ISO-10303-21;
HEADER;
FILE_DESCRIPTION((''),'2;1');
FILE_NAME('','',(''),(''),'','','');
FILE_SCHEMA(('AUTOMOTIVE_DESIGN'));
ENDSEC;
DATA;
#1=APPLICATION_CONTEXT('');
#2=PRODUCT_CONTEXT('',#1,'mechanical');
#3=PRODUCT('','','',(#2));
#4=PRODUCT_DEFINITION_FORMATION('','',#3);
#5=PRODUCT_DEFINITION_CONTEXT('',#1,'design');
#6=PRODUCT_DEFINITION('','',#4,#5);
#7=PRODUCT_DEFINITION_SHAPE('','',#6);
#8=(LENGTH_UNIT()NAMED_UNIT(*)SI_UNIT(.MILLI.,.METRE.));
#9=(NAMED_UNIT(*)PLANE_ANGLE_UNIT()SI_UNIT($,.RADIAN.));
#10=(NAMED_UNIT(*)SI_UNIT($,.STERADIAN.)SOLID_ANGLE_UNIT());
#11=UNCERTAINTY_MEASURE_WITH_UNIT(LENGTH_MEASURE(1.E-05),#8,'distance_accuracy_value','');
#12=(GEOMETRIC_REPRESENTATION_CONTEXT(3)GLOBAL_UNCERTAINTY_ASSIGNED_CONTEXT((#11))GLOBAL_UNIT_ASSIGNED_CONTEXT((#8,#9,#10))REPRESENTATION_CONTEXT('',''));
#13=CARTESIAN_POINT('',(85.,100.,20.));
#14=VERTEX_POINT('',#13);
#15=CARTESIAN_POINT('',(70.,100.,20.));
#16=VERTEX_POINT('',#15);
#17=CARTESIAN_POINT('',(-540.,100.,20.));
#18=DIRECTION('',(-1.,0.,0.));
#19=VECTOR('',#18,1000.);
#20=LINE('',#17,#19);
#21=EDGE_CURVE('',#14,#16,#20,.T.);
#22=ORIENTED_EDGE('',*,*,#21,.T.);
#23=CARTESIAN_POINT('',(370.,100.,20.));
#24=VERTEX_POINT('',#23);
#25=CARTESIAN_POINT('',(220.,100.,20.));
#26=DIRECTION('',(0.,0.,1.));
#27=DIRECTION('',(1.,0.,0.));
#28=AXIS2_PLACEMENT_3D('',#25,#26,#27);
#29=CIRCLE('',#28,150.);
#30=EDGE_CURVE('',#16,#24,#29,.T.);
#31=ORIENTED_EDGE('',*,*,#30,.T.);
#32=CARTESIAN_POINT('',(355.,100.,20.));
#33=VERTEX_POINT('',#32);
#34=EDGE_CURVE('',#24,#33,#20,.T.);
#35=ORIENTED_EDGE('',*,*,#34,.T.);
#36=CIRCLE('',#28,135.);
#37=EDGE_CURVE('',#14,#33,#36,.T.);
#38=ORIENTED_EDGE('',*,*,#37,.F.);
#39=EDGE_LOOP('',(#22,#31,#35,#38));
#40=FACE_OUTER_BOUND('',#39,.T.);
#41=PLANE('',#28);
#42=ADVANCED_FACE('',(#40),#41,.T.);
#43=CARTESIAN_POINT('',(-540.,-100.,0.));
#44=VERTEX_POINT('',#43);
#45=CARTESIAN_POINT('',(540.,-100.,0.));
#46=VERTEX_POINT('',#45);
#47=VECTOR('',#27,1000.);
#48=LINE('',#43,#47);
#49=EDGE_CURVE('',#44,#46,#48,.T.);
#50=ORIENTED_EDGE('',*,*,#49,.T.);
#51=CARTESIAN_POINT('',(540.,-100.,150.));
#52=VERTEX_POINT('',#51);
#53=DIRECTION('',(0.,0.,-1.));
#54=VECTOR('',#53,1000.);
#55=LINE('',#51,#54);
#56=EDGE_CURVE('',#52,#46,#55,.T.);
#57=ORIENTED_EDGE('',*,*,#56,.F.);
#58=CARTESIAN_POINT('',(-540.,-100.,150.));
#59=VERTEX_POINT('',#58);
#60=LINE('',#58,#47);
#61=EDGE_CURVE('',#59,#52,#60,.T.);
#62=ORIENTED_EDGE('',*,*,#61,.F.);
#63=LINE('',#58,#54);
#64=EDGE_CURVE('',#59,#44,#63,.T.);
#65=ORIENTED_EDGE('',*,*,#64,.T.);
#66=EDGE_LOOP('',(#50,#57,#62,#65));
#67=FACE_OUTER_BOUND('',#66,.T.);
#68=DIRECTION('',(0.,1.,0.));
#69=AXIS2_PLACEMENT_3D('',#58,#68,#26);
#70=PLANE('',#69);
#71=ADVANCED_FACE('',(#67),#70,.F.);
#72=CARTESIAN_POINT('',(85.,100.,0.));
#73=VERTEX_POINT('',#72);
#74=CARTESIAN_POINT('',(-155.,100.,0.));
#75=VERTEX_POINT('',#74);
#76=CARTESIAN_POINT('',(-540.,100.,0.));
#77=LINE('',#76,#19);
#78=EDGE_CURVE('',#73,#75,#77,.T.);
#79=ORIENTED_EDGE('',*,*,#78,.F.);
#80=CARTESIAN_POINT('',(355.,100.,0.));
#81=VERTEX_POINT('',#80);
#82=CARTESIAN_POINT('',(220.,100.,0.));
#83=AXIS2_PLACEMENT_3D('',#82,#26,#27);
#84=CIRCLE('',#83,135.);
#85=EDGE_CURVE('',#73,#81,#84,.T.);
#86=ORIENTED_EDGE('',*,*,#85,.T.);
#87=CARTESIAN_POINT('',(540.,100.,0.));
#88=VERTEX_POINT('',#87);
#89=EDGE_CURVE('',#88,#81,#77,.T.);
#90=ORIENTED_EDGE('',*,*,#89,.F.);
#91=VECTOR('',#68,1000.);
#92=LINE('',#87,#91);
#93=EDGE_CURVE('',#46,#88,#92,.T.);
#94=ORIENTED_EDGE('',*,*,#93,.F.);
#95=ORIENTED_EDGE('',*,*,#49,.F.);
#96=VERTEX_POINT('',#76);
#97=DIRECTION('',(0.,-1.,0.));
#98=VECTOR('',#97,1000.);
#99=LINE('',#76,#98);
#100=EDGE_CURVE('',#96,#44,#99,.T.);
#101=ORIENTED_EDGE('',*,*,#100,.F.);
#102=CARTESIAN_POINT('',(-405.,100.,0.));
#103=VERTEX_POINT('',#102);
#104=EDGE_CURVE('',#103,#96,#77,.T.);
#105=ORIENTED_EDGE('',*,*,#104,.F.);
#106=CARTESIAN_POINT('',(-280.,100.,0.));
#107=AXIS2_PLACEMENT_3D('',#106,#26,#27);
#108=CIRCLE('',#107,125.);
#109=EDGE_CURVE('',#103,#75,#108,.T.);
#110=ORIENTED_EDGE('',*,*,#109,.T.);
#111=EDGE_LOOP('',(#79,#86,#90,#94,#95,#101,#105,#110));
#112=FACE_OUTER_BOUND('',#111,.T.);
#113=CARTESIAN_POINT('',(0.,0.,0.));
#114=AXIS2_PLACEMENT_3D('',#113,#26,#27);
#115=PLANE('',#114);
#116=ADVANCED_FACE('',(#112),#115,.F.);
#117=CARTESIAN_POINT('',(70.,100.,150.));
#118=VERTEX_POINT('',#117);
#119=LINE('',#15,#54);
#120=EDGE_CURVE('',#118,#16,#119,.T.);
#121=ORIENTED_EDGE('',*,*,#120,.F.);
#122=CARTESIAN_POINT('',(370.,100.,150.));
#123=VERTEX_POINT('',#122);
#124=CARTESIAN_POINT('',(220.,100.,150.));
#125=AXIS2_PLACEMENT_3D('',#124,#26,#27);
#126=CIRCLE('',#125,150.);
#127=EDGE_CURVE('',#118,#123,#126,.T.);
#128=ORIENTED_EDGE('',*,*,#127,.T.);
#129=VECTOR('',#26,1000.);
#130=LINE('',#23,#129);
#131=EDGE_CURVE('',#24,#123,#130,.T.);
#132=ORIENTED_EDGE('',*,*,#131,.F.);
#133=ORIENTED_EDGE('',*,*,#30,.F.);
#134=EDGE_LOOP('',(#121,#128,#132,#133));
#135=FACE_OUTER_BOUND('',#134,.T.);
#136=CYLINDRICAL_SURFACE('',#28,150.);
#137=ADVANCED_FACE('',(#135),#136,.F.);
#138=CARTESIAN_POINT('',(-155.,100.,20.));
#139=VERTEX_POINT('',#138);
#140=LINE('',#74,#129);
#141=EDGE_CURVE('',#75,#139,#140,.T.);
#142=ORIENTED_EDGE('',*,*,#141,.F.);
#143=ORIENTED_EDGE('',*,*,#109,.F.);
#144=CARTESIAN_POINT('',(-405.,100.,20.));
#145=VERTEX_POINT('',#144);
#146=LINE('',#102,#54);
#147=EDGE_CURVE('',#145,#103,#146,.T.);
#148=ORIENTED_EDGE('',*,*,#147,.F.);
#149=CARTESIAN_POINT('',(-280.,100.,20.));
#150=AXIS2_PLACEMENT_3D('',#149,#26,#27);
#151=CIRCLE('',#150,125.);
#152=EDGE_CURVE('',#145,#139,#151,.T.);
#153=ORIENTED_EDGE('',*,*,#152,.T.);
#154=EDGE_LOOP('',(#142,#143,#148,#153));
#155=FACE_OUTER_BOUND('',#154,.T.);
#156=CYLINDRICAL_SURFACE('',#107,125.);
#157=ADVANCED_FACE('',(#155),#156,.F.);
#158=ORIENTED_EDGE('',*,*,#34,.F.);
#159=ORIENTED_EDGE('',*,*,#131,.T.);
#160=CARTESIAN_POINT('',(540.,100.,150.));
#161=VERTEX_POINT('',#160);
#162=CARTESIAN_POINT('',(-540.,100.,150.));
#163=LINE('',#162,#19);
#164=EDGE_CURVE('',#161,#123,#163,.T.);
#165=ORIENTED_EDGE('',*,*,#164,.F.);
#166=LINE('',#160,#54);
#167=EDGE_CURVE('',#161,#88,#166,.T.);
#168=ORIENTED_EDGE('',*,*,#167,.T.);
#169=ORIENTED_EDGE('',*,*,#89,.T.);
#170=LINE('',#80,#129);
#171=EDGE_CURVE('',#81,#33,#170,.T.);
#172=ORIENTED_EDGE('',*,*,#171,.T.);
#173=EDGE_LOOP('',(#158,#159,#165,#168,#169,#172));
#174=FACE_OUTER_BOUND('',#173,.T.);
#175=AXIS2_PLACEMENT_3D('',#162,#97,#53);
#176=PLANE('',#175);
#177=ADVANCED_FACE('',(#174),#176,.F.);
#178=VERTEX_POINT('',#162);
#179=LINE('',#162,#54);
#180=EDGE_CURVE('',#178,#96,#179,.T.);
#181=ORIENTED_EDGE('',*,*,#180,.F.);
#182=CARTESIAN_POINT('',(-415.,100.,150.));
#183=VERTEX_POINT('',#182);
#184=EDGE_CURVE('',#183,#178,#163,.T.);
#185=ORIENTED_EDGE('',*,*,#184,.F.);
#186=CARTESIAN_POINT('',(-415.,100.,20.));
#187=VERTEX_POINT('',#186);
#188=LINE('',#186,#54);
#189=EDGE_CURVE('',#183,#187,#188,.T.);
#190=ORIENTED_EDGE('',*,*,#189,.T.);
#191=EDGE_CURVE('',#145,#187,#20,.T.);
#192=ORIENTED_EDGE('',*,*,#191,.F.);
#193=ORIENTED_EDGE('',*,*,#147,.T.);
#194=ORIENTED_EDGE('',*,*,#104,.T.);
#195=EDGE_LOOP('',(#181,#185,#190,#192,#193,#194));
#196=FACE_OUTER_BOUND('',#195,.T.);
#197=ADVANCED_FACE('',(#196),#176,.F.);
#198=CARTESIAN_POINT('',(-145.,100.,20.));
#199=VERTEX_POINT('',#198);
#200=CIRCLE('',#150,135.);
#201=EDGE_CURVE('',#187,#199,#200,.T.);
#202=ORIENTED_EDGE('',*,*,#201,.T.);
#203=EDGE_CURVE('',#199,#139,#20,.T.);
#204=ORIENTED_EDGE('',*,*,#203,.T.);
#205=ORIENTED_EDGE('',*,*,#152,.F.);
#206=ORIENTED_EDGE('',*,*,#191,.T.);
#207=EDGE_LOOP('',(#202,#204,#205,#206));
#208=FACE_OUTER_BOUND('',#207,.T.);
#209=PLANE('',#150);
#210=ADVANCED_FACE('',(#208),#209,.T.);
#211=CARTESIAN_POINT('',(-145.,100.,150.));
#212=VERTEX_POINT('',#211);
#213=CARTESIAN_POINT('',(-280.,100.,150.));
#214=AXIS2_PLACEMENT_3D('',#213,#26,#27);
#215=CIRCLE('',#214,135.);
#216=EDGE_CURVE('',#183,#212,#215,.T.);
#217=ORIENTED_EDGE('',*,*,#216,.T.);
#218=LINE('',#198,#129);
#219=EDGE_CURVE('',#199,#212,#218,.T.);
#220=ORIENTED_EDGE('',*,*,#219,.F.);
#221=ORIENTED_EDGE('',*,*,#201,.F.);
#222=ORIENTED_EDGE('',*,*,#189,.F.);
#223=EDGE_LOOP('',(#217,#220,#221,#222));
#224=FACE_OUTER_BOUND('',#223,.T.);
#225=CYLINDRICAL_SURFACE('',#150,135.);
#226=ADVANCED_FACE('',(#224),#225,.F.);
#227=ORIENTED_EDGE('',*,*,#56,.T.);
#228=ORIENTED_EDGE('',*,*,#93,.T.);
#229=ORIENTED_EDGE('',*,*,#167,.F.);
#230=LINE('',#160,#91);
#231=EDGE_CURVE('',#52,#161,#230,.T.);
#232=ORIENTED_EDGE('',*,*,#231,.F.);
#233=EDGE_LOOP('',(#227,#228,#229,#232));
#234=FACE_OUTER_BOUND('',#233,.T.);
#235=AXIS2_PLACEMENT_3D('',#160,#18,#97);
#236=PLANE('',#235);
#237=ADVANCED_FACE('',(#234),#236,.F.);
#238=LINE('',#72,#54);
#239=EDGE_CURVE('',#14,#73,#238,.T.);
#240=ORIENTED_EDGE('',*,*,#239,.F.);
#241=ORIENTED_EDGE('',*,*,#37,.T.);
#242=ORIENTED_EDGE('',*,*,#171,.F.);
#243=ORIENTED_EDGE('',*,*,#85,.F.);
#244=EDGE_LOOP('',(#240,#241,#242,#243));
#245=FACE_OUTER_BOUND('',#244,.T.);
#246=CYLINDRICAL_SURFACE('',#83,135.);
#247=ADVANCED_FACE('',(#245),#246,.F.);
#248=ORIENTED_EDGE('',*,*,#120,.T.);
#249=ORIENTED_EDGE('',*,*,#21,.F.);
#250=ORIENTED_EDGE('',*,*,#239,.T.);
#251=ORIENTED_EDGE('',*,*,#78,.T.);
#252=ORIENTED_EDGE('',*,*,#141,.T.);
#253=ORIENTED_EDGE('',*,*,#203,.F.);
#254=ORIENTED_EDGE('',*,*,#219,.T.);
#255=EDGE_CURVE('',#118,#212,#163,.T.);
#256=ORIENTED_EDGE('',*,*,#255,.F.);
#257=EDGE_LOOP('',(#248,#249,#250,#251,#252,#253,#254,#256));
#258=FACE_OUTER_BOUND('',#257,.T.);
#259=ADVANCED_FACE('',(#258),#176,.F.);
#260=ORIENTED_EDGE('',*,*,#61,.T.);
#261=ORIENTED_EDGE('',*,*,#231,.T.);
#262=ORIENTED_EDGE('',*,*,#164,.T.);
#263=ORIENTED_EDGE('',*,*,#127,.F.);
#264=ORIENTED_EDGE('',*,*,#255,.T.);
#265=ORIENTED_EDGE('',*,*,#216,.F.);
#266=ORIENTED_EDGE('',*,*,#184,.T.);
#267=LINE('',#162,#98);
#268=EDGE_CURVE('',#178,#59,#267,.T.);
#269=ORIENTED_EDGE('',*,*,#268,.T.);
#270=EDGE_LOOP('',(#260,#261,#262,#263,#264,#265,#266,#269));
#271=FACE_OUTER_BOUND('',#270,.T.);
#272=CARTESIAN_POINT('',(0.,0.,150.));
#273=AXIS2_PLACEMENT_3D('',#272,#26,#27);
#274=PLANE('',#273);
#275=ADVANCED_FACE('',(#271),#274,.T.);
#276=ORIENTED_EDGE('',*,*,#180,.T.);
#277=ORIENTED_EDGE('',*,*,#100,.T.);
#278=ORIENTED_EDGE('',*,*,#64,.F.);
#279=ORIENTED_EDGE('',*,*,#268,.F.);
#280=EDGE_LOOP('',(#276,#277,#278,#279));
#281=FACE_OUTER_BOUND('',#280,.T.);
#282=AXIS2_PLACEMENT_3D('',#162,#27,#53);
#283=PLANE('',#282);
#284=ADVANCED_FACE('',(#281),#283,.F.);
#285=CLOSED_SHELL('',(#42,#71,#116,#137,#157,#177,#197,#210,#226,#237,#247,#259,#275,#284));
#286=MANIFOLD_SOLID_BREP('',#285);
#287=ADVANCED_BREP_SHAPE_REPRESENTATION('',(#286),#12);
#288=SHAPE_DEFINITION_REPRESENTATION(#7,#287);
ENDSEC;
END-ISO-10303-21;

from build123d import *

# Parameters (mm, degrees)
SKETCH1_W               = 1080
SKETCH1_H               = 200
BOSS_EXTRUDE1_DEPTH     = 150
SKETCH_2_3_R            = 135
SKETCH_2_3_R_2          = 150
CUT_EXTRUDE1_DEPTH      = 130
CUT_EXTRUDE2_DEPTH      = 570.2978131
CUT_EXTRUDE2_DEPTH_BACK = 570.2978131
SKETCH_2_3_2_R          = 125
SKETCH_2_3_2_R_2        = 135


with BuildPart() as part:
    # Sketch1 → Boss-Extrude1 (new body)
    with BuildSketch(Plane.XY):
        Rectangle(SKETCH1_W, SKETCH1_H)
    extrude(amount=BOSS_EXTRUDE1_DEPTH)

    # Sketch 2_3 → Cut-Extrude1 (cut)
    with BuildSketch(Plane.XY.offset(150)):
        with Locations((-280, 100)):
            Circle(SKETCH_2_3_R)
        with Locations((220, 100)):
            Circle(SKETCH_2_3_R_2)
    extrude(amount=-CUT_EXTRUDE1_DEPTH, mode=Mode.SUBTRACT)

    # Sketch 2_3 2 → Cut-Extrude2 (cut, two sides: drawn at the far end of the back side and taken through both)
    with BuildSketch(Plane.XY.offset(150).offset(-CUT_EXTRUDE2_DEPTH_BACK)):
        with Locations((-280, 100)):
            Circle(SKETCH_2_3_2_R)
        with Locations((220, 100)):
            Circle(SKETCH_2_3_2_R_2)
    extrude(amount=CUT_EXTRUDE2_DEPTH + CUT_EXTRUDE2_DEPTH_BACK, mode=Mode.SUBTRACT)


solid = part.part
